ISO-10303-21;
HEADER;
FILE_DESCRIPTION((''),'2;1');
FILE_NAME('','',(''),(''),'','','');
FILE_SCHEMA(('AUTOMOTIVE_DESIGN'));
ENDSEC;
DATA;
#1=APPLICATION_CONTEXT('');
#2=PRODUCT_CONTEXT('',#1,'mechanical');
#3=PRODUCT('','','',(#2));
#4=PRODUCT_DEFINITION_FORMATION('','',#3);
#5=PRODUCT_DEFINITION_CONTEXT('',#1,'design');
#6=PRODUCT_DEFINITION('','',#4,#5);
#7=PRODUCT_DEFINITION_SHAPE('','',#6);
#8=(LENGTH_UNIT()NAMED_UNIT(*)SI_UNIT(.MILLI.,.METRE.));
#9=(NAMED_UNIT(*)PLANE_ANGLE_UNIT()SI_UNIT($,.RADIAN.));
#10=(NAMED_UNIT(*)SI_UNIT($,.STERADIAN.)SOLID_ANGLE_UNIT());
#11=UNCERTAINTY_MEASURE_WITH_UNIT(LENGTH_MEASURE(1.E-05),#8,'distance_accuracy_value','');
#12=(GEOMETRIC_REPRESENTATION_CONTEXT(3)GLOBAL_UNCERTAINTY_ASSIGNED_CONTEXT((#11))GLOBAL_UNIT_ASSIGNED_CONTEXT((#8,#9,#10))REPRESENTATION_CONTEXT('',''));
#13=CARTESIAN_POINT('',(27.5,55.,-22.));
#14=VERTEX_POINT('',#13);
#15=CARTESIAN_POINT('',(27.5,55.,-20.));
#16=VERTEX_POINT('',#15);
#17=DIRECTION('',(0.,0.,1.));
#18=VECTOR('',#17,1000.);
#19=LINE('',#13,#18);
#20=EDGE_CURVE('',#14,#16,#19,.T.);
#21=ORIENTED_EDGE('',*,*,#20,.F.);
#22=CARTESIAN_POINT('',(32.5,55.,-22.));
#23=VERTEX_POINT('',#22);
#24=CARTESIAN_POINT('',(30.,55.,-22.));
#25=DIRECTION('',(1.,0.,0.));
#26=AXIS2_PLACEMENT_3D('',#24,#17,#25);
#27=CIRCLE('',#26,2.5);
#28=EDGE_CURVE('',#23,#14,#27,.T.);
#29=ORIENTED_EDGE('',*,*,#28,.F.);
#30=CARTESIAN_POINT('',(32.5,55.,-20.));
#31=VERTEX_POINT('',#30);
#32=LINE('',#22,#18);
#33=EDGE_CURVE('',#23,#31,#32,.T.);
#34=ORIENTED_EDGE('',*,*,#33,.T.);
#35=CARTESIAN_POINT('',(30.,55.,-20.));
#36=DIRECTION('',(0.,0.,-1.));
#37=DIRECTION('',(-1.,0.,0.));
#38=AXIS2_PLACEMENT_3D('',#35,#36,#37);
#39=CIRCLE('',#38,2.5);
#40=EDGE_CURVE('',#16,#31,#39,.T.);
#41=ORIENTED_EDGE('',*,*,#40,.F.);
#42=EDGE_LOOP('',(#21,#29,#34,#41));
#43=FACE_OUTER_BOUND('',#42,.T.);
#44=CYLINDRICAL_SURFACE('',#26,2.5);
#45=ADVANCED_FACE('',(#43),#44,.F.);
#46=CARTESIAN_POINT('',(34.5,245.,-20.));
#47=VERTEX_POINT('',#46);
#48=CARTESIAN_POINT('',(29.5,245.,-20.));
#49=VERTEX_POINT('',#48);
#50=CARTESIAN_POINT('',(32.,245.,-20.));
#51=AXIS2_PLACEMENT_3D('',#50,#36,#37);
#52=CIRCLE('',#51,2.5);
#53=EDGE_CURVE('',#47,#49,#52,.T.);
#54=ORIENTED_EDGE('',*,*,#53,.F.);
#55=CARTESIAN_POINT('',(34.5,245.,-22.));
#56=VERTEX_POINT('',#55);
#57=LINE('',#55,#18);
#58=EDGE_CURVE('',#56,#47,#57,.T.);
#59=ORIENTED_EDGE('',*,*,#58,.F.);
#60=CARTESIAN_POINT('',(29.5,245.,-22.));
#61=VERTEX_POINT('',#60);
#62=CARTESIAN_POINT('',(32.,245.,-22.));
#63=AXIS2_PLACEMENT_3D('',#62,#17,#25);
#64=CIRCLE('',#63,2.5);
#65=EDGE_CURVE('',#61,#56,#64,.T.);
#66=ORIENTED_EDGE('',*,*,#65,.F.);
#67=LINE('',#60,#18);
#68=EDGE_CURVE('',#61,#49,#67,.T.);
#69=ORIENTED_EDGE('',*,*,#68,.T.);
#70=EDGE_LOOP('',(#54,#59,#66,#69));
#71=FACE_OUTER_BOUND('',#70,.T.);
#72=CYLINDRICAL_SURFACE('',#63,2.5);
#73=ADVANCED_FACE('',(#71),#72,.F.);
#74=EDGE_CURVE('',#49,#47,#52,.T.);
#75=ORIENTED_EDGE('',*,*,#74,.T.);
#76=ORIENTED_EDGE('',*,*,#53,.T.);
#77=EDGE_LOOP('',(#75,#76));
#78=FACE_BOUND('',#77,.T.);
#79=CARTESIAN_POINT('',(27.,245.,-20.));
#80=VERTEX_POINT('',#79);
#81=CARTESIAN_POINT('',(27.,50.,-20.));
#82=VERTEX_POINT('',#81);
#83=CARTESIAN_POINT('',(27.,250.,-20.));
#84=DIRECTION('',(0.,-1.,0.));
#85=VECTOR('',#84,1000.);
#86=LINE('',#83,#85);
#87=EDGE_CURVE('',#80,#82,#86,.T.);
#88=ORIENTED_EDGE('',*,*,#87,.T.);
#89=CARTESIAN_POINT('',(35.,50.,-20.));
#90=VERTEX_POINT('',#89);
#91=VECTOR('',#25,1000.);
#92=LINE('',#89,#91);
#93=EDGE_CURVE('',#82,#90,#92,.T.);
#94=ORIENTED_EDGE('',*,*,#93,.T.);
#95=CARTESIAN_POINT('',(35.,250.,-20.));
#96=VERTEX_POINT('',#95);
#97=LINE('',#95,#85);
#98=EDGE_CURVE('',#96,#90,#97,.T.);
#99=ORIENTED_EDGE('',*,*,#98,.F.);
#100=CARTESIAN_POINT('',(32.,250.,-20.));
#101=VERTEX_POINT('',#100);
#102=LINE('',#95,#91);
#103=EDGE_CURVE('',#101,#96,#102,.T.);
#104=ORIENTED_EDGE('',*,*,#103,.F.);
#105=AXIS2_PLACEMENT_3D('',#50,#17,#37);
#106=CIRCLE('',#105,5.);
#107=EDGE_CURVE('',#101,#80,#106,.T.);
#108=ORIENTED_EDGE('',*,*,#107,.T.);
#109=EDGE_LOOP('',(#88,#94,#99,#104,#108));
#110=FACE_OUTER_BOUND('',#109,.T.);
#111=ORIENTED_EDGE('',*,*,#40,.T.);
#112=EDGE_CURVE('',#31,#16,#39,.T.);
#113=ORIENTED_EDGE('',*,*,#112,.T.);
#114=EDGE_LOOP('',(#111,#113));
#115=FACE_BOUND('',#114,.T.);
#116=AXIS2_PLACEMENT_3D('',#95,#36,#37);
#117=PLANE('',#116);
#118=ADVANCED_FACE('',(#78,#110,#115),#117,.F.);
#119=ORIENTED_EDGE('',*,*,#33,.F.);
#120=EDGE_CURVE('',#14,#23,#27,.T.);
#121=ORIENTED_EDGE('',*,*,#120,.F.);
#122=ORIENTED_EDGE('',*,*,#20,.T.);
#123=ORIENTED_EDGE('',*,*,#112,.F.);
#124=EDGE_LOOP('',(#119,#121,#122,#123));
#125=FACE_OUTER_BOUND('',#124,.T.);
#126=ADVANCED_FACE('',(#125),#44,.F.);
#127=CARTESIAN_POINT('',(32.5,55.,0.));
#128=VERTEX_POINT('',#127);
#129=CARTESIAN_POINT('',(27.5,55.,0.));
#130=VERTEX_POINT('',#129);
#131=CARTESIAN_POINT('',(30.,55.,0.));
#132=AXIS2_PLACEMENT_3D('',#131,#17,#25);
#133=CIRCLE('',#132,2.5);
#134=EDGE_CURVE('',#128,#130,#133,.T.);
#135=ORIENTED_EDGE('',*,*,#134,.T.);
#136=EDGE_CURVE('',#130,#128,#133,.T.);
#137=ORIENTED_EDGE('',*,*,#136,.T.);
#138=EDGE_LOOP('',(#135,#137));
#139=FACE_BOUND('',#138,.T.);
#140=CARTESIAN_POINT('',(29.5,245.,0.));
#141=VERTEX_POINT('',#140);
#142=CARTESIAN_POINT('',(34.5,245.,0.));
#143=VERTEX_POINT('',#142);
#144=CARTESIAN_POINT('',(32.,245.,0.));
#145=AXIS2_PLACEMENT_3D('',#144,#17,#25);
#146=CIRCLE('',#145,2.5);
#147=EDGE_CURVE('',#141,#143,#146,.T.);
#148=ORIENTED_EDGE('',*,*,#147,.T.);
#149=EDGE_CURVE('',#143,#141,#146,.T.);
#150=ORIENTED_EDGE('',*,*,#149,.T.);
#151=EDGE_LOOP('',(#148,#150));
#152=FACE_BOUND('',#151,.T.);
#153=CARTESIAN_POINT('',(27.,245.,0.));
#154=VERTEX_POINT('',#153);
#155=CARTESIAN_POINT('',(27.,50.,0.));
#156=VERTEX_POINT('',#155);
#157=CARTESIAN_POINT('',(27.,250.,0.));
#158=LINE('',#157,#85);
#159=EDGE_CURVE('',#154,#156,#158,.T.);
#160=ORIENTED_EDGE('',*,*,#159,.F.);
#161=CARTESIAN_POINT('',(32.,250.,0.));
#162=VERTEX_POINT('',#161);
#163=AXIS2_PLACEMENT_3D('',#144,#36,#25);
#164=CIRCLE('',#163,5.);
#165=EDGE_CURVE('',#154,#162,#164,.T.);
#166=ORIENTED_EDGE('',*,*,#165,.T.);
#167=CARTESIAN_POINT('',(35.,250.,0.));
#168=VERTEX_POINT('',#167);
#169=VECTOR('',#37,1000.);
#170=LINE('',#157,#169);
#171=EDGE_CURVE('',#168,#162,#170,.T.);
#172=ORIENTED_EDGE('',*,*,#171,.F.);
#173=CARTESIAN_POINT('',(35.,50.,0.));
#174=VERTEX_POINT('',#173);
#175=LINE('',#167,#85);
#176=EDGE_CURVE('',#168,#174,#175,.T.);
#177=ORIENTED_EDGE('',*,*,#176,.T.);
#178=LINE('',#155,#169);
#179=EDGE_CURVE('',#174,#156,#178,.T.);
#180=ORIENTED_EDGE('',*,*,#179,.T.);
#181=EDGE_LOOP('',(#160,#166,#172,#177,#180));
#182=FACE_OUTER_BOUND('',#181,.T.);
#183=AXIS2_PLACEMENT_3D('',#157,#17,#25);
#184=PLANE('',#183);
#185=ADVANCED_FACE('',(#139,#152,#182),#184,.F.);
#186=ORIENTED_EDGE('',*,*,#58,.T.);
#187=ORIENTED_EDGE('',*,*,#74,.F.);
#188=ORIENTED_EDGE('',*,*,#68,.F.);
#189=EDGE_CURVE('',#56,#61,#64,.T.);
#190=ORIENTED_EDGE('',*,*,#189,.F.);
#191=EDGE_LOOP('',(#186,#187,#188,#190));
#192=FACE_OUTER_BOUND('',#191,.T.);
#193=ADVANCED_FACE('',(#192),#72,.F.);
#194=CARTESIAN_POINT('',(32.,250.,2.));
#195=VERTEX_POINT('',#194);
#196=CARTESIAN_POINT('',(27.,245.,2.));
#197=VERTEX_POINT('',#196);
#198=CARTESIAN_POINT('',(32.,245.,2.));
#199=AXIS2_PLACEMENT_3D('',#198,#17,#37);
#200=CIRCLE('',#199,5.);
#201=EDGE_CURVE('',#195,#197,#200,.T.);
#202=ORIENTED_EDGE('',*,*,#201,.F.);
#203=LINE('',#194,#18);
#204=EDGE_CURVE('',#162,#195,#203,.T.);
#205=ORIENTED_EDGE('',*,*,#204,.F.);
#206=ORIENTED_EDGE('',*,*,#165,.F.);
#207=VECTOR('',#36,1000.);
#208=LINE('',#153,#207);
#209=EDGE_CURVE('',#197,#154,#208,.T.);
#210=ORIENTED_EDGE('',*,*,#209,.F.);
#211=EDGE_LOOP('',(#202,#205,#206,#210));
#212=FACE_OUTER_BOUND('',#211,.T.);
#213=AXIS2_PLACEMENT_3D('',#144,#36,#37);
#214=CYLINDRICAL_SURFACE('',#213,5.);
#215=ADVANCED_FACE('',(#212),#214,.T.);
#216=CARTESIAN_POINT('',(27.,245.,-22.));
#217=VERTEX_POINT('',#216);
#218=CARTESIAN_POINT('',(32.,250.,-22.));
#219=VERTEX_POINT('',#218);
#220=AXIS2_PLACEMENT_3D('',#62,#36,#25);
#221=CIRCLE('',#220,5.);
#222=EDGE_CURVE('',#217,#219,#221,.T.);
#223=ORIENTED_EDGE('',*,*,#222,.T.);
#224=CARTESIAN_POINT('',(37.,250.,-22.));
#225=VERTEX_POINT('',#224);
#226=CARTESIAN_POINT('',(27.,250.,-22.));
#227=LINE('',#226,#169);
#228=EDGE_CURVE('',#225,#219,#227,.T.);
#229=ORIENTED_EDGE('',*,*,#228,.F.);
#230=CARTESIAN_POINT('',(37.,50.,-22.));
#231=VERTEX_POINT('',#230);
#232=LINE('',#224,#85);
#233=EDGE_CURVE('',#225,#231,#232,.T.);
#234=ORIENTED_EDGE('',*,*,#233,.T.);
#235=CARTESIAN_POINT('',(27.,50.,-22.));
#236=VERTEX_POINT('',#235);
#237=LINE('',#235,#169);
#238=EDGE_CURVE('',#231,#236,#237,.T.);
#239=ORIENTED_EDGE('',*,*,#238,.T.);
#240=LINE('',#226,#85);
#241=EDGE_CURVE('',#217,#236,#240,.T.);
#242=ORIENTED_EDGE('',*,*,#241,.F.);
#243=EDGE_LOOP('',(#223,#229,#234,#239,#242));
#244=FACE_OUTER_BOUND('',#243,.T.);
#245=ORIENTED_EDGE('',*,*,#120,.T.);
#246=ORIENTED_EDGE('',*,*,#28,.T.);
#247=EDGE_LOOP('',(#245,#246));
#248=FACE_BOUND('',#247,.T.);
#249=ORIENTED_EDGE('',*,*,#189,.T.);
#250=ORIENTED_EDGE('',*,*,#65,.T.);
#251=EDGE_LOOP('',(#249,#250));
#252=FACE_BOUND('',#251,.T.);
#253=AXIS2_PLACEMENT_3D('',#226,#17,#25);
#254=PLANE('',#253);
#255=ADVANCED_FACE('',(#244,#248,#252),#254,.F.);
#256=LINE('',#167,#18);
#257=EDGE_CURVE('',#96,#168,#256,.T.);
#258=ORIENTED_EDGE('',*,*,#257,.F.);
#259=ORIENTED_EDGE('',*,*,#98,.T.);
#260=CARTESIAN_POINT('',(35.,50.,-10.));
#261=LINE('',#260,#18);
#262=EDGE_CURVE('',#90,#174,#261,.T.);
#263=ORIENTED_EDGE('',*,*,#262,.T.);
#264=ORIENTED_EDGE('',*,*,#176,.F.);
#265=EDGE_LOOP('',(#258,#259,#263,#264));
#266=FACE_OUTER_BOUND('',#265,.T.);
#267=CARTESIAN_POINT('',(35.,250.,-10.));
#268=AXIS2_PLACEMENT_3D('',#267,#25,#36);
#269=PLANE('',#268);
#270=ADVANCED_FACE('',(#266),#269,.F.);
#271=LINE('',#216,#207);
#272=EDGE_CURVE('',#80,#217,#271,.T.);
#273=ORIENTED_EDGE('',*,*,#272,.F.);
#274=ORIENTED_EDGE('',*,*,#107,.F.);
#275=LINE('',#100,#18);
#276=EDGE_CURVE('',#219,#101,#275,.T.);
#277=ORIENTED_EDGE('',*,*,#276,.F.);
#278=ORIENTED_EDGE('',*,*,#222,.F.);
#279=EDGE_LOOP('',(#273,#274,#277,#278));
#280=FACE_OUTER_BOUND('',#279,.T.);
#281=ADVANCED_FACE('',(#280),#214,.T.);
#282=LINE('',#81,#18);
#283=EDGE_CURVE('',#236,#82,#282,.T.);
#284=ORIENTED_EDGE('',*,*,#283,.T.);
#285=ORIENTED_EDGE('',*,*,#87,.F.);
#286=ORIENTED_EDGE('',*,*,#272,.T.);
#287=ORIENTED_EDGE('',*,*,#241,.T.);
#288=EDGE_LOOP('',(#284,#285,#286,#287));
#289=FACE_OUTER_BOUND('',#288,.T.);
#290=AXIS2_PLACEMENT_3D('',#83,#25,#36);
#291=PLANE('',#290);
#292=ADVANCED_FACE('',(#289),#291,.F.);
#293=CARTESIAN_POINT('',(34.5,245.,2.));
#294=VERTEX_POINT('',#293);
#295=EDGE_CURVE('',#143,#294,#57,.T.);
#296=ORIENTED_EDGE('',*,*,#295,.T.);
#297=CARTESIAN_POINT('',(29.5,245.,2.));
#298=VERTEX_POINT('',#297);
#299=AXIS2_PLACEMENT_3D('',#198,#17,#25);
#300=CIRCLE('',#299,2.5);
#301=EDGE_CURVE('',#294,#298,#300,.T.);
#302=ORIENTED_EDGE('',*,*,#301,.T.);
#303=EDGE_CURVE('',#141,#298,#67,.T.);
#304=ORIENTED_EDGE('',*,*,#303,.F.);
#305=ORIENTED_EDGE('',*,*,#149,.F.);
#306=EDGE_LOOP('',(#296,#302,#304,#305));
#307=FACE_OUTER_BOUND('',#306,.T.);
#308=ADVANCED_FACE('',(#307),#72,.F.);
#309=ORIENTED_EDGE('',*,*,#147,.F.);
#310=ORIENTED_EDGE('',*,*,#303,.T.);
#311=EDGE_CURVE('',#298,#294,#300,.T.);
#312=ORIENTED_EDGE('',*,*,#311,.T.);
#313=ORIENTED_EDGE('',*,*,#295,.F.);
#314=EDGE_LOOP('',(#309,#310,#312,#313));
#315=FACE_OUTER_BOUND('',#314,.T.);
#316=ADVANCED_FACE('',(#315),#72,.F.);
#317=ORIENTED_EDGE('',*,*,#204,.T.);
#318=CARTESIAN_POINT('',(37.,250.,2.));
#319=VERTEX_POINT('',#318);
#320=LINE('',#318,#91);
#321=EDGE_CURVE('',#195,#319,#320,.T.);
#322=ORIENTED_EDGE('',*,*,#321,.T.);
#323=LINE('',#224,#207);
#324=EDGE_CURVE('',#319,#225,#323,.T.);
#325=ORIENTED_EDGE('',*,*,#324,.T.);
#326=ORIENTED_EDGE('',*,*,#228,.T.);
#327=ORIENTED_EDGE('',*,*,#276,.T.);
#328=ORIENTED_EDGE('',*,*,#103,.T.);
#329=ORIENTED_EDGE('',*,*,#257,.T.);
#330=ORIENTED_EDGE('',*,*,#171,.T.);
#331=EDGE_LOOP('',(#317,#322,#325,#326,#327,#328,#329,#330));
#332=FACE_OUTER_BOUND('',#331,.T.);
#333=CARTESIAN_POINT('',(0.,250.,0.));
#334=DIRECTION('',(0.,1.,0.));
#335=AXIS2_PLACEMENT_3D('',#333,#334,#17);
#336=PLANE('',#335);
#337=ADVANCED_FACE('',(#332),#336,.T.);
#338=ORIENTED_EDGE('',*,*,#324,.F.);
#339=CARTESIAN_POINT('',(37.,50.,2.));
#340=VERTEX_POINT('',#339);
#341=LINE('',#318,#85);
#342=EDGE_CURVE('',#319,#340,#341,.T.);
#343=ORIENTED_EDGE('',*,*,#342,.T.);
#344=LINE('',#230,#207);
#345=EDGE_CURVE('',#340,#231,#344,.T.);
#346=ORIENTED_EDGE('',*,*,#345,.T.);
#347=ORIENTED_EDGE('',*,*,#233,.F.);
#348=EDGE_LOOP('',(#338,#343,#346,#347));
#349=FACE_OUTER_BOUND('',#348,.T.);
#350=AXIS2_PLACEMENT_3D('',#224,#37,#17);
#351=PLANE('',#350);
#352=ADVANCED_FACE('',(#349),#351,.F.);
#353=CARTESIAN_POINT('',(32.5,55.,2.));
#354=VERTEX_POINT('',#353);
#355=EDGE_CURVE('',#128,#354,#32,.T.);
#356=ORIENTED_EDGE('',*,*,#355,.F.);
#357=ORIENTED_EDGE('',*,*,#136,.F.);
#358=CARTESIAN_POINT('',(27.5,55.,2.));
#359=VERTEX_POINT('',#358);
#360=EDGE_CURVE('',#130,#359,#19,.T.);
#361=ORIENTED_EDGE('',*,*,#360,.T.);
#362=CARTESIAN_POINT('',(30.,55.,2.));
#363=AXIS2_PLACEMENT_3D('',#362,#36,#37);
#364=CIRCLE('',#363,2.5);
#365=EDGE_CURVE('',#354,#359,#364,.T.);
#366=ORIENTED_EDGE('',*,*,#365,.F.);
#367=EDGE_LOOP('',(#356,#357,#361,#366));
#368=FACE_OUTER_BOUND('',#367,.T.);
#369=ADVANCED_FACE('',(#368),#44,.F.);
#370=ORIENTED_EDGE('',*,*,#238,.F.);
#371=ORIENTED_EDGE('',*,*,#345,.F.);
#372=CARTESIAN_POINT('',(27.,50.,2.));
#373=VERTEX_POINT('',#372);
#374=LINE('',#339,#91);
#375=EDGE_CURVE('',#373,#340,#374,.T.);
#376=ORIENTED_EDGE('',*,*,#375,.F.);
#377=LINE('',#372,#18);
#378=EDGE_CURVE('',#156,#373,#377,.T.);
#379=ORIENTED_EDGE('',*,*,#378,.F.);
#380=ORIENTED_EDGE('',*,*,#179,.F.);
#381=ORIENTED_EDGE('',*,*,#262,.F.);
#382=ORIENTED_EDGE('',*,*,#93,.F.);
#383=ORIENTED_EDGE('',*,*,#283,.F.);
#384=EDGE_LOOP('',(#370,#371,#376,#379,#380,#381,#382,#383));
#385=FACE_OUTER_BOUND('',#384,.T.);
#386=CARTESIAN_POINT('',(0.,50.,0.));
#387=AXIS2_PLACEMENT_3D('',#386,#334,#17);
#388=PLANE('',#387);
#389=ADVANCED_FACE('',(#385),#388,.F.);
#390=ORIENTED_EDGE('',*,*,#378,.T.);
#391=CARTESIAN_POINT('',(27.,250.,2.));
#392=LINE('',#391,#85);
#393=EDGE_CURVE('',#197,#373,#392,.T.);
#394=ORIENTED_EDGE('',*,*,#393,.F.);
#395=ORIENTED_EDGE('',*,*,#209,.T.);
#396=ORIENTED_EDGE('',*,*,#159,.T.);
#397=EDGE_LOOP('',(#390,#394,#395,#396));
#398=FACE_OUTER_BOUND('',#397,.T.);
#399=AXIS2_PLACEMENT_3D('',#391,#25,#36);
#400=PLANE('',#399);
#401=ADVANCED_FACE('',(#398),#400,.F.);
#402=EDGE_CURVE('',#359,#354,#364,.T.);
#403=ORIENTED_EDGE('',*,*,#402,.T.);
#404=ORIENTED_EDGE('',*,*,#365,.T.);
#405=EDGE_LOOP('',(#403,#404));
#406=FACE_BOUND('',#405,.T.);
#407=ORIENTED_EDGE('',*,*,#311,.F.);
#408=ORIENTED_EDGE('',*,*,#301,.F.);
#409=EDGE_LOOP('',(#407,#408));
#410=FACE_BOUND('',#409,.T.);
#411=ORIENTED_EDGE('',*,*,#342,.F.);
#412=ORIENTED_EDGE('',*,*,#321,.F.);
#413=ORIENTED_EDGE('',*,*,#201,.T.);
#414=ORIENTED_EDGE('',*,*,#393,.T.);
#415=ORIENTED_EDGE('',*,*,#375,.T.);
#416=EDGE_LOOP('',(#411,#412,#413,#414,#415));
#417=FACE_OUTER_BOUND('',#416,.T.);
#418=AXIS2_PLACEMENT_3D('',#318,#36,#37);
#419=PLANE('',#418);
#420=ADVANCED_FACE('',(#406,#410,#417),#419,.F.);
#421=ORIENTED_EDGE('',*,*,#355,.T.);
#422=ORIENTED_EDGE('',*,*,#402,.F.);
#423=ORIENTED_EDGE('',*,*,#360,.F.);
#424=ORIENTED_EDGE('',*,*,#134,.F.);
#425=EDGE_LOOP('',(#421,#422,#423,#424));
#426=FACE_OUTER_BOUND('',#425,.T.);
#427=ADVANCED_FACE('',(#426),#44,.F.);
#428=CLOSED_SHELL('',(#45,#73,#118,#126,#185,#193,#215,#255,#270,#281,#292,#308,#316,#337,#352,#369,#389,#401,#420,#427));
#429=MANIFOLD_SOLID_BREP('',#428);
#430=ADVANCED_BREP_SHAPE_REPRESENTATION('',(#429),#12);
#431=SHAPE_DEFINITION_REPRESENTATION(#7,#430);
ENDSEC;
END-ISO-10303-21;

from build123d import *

# Parameters (mm, degrees)
BOSS_EXTRUDE1_DEPTH     = 200
CUT_EXTRUDE1_DEPTH      = 254.860197747
CUT_EXTRUDE1_DEPTH_BACK = 254.860197747
SKETCH3_R               = 2.5
FILLET1_R               = 5
CUT_EXTRUDE2_DEPTH      = 254.860197747
CUT_EXTRUDE2_DEPTH_BACK = 254.860197747
SKETCH5_R               = 2.5


with BuildPart() as part:
    # Sketch2 → Boss-Extrude1 (new body)
    with BuildSketch(Plane(origin=(0, 50, 0), x_dir=(1, 0, 0), z_dir=(0, 1, 0))):
        Polygon((35, 10), (35, 20), (27, 20), (27, 22), (37, 22), (37, -2), (27, -2), (27, 0), (35, 0), align=None)
    extrude(amount=BOSS_EXTRUDE1_DEPTH)

    # Sketch3 → Cut-Extrude1 (cut, two sides: drawn at the far end of the back side and taken through both)
    with BuildSketch(Plane.XY.offset(2).offset(-CUT_EXTRUDE1_DEPTH_BACK)):
        with Locations((30, 55)):
            Circle(SKETCH3_R)
    extrude(amount=CUT_EXTRUDE1_DEPTH + CUT_EXTRUDE1_DEPTH_BACK, mode=Mode.SUBTRACT)

    # Fillet1
    fillet1_edges = [part.edges().sort_by_distance(p)[0] for p in [
        (27, 250, 1),
        (27, 250, -21),
    ]]
    fillet(fillet1_edges, radius=FILLET1_R)

    # Sketch5 → Cut-Extrude2 (cut, two sides: drawn at the far end of the back side and taken through both)
    with BuildSketch(Plane.XY.offset(2).offset(-CUT_EXTRUDE2_DEPTH_BACK)):
        with Locations((32, 245)):
            Circle(SKETCH5_R)
    extrude(amount=CUT_EXTRUDE2_DEPTH + CUT_EXTRUDE2_DEPTH_BACK, mode=Mode.SUBTRACT)


solid = part.part
